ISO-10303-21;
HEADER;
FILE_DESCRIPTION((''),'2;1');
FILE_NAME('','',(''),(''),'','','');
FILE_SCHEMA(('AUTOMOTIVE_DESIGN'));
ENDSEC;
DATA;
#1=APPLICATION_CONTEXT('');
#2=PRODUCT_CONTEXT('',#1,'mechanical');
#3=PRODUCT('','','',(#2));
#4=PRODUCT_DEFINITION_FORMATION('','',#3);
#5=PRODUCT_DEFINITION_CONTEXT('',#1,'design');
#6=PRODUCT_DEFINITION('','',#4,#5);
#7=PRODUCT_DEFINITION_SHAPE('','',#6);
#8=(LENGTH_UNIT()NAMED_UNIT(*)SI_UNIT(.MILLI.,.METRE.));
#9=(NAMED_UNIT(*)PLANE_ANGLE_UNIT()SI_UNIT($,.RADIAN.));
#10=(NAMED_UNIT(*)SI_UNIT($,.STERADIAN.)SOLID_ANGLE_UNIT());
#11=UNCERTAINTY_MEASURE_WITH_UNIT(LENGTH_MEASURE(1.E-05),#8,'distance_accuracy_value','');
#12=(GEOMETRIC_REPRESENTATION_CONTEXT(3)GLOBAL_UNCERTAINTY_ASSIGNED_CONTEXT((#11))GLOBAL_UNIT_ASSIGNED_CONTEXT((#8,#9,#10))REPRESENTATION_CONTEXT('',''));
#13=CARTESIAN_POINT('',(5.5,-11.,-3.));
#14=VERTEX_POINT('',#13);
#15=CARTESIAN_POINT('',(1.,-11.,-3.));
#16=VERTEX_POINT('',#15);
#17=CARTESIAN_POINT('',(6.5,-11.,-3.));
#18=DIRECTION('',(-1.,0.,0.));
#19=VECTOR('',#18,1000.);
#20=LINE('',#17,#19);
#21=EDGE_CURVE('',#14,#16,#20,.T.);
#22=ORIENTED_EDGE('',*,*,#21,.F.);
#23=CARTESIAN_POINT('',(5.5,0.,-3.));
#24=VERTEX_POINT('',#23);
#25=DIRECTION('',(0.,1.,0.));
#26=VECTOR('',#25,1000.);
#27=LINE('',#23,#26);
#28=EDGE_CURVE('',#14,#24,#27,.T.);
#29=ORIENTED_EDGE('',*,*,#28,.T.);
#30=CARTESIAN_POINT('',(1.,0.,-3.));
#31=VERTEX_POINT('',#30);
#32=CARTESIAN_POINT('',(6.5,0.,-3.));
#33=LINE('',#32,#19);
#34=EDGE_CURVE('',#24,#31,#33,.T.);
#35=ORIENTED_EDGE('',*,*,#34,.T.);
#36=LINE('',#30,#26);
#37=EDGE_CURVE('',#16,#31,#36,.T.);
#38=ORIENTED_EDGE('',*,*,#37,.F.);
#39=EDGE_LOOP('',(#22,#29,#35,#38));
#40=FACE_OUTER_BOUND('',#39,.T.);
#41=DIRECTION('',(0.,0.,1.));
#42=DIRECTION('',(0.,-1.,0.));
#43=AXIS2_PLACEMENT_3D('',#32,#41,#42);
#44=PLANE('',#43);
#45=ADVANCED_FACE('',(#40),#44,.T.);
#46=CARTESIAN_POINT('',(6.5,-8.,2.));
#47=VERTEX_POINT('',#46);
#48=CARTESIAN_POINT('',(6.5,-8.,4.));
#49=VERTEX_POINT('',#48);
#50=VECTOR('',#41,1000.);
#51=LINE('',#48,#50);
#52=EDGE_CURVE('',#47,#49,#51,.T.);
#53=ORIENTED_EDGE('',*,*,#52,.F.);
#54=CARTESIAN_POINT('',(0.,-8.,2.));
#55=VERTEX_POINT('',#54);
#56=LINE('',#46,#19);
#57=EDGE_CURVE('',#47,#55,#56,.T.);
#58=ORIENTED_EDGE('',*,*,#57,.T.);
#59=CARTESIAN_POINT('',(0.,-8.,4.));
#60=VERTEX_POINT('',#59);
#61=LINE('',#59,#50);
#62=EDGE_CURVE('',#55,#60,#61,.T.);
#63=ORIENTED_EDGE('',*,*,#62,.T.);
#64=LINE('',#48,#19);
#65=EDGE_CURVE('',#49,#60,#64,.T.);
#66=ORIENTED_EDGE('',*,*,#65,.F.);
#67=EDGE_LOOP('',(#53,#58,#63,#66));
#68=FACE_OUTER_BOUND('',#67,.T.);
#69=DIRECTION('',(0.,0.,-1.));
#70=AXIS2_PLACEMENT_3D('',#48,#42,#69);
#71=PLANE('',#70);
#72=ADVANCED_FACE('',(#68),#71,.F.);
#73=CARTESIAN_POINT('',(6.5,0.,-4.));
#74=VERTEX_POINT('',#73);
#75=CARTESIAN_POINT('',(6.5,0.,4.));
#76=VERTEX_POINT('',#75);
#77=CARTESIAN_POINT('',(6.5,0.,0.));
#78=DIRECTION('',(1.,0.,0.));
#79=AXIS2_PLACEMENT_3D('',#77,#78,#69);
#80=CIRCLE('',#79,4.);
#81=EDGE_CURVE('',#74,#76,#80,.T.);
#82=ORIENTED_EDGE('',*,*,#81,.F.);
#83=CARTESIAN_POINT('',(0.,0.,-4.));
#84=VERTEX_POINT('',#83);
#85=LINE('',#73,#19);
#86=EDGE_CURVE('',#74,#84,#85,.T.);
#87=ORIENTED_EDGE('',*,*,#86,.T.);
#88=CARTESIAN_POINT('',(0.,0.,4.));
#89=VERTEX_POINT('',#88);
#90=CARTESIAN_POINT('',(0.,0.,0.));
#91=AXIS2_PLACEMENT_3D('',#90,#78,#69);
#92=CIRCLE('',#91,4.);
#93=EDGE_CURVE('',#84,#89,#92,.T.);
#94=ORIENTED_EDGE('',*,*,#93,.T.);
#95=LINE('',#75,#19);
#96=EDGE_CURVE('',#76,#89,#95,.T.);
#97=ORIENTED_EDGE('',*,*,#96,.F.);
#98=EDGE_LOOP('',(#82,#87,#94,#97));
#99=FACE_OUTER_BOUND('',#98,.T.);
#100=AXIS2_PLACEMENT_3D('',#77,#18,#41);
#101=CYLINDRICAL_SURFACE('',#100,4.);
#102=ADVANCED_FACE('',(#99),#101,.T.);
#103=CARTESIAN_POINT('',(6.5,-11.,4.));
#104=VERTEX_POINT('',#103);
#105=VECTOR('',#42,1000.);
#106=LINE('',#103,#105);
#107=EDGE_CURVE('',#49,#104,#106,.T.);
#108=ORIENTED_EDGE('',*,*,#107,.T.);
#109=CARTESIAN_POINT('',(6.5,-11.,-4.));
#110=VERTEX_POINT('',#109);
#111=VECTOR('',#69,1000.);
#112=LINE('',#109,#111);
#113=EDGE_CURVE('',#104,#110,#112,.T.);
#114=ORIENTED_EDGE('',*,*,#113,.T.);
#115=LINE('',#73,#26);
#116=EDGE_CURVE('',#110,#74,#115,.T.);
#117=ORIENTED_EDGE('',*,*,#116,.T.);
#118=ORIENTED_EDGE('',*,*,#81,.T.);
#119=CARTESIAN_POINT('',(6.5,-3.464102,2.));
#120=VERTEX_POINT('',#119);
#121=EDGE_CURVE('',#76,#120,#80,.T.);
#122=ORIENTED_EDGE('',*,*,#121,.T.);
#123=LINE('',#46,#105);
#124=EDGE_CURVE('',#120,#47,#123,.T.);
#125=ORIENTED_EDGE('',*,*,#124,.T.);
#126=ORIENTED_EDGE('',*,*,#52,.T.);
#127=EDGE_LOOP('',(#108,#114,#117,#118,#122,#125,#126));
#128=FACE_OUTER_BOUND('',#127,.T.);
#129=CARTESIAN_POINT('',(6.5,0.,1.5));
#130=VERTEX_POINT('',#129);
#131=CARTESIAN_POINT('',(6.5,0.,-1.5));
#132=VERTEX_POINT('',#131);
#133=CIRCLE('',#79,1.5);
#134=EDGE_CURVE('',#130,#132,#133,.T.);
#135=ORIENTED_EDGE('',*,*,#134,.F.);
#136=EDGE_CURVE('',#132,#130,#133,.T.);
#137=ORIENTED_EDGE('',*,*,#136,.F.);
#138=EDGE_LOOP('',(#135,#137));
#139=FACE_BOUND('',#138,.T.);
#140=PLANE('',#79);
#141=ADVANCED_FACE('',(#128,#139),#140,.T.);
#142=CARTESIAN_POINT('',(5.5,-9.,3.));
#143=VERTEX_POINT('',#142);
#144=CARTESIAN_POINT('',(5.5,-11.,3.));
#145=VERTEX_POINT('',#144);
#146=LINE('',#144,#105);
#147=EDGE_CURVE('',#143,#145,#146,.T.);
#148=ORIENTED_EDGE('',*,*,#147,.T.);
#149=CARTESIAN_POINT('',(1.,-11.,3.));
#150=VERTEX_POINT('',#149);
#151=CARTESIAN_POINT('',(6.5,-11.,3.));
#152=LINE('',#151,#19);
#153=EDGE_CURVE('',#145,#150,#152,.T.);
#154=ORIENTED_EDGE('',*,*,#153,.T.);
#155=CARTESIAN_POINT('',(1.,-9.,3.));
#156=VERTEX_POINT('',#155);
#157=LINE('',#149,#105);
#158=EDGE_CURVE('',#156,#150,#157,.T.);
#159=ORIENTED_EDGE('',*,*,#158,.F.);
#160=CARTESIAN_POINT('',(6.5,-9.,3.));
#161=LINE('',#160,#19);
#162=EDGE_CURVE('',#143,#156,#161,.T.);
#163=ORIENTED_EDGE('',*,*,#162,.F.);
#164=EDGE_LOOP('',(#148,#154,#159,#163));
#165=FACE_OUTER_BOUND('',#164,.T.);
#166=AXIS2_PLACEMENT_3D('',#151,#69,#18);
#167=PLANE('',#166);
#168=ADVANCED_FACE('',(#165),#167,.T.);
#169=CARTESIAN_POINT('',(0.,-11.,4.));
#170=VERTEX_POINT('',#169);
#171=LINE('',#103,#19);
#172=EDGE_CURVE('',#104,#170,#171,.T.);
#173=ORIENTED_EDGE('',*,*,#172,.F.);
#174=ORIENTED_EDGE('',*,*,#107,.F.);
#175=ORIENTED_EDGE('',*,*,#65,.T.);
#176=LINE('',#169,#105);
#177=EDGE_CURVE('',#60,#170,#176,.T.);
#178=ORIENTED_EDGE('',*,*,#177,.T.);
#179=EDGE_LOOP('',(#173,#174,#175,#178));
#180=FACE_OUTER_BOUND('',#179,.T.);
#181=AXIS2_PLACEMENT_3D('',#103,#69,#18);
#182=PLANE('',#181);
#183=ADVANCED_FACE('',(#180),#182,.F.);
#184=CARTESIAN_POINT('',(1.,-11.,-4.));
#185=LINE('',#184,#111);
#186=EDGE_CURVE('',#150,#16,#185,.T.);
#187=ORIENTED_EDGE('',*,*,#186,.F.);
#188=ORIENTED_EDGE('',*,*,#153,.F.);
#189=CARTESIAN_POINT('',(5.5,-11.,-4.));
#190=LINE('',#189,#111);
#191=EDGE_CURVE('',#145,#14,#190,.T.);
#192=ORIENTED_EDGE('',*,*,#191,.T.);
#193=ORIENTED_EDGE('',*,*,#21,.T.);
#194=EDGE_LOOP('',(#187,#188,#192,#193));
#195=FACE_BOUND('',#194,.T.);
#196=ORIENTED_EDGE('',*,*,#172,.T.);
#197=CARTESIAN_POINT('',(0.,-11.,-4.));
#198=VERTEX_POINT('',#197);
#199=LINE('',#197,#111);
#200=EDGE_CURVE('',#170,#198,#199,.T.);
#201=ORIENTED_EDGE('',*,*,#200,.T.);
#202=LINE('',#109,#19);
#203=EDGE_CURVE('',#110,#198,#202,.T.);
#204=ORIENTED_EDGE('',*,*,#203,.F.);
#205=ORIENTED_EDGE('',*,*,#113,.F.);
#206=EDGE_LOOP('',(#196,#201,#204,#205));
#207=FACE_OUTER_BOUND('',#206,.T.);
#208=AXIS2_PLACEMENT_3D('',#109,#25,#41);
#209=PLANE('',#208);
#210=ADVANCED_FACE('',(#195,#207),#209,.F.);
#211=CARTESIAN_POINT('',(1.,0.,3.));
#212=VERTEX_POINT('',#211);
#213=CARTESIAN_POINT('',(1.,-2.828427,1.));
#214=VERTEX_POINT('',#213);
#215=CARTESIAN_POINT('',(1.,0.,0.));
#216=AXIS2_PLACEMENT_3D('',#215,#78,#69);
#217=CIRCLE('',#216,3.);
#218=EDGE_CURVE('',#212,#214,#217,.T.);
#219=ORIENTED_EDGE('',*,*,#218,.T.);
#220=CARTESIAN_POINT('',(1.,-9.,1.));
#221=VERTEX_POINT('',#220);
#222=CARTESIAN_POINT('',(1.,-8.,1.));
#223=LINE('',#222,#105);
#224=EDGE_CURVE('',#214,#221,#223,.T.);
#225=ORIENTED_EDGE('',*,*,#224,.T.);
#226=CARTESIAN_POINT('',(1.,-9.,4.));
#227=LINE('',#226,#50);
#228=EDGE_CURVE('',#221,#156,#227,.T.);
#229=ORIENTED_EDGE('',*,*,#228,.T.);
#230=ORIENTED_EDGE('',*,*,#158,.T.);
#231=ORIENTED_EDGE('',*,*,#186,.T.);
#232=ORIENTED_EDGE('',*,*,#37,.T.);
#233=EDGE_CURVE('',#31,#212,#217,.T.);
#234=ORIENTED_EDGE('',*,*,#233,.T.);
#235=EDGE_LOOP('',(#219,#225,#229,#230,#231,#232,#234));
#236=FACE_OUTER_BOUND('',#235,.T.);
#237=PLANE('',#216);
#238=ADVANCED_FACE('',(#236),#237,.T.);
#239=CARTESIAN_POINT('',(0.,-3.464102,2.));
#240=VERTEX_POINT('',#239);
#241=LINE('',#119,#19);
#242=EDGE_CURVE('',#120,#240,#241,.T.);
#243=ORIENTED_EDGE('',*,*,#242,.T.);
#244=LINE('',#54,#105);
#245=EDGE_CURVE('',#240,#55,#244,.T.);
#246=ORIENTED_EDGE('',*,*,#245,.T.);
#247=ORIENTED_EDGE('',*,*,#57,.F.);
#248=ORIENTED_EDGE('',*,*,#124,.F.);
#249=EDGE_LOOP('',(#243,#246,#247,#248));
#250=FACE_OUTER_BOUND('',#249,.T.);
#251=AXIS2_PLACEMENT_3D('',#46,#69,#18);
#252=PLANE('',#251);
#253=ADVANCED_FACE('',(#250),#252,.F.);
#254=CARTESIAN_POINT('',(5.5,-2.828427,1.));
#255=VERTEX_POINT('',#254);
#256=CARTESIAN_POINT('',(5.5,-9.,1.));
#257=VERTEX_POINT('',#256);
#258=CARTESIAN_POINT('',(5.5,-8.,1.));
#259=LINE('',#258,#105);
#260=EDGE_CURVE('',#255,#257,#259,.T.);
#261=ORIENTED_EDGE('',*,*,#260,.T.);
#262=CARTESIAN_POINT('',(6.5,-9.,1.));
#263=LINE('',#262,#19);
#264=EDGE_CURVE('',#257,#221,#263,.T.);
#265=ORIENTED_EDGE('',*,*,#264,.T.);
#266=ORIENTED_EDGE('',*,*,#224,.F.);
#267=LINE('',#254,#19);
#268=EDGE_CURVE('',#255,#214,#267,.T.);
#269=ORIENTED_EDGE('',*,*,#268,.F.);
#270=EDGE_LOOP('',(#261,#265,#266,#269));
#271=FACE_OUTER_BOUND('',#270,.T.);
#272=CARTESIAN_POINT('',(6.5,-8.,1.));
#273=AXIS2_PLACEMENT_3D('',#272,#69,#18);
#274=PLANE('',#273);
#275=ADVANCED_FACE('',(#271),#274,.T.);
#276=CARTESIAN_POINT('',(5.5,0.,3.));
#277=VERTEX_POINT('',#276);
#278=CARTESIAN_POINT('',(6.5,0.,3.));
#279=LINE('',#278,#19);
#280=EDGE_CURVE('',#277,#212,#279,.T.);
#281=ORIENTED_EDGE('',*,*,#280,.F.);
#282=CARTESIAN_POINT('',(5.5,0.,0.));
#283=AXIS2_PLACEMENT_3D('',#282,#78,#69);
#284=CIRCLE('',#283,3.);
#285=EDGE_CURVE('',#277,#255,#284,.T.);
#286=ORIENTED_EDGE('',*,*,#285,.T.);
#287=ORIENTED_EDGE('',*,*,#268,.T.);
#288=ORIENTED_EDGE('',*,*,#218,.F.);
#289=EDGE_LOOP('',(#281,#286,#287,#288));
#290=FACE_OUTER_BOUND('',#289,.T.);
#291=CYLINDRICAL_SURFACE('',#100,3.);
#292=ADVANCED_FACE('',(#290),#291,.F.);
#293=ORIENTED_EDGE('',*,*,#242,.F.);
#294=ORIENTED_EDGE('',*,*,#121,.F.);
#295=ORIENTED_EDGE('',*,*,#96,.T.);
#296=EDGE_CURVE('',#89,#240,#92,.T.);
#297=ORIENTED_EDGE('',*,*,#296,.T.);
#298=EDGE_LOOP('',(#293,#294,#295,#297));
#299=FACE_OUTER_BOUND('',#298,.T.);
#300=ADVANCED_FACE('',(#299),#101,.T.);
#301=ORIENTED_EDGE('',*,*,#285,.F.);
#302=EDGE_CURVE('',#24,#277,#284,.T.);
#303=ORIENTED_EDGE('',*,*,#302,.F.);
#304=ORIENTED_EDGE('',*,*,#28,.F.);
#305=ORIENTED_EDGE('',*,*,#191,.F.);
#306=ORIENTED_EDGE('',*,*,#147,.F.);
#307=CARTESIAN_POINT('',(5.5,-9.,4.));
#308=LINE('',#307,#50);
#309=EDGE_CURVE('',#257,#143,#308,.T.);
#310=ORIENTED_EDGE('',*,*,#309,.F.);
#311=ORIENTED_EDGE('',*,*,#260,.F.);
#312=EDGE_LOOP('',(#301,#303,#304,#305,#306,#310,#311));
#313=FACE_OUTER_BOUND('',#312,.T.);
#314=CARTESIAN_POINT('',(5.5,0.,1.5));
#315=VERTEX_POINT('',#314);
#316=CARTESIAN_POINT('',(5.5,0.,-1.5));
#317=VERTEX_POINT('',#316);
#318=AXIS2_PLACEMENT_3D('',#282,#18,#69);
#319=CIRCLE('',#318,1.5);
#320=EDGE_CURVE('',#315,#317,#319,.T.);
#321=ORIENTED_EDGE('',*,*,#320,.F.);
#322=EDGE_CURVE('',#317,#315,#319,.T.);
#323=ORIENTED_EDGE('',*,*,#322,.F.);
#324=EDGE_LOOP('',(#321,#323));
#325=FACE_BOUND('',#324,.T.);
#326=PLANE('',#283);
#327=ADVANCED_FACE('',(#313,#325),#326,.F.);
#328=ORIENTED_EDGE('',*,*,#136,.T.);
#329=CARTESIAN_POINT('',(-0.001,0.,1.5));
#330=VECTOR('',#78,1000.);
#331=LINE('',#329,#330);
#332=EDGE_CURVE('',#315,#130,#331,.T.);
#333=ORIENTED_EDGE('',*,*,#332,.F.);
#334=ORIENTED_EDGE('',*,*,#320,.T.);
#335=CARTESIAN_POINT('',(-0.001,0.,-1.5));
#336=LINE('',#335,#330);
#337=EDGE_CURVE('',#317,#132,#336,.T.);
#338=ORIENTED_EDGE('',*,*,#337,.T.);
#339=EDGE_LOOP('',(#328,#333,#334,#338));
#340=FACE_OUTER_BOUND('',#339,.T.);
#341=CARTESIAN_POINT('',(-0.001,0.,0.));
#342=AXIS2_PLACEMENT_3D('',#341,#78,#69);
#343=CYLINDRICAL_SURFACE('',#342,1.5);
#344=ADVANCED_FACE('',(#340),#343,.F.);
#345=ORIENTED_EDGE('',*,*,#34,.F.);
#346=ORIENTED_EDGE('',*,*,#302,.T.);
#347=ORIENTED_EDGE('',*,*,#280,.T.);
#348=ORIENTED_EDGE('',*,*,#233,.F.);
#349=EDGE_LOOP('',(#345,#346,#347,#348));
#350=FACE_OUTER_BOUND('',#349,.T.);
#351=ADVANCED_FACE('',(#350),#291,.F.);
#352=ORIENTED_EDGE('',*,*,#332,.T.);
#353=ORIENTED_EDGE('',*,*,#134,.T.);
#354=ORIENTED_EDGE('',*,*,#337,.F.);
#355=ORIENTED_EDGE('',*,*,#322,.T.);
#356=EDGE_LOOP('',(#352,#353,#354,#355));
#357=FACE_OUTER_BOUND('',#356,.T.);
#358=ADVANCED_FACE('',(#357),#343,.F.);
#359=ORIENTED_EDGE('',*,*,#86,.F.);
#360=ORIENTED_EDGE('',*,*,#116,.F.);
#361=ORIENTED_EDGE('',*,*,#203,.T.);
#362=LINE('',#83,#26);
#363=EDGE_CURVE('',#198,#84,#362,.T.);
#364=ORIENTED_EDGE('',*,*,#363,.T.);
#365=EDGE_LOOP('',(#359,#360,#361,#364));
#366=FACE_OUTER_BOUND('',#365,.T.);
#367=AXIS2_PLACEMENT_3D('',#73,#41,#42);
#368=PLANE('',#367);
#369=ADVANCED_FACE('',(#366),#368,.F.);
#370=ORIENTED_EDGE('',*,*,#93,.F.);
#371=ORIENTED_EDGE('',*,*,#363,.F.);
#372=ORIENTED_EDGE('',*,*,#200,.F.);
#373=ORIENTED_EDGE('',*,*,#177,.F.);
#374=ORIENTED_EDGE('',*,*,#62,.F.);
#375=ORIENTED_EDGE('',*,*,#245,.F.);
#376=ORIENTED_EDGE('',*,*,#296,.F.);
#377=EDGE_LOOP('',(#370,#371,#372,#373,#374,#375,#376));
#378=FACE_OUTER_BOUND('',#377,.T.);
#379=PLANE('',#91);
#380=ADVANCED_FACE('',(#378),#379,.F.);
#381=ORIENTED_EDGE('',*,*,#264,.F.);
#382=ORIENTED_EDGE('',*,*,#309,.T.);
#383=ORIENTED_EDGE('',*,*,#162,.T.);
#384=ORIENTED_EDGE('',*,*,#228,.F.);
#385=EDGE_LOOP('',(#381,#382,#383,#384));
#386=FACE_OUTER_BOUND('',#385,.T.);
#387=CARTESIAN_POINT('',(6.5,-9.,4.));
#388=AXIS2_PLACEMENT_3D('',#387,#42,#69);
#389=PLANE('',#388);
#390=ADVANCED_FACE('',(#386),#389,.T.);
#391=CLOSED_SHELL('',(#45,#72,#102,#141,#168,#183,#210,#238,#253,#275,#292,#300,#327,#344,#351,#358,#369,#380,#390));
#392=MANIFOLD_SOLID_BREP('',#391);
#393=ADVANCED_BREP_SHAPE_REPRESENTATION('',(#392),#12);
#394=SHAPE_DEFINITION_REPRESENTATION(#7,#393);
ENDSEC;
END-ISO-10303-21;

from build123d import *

# Parameters (mm, degrees)
LEG_BODY_DEPTH        = 6.5
LEG_SHELL_1MM_T       = -1
HIP_PIN_HOLE_REACH    = 15.388
HIP_PIN_HOLE_SKETCH_R = 1.5


with BuildPart() as part:
    # Leg Profile Sketch → Leg Body (new body)
    with BuildSketch(Plane(origin=(0, 0, 0), x_dir=(0, 0, -1), z_dir=(1, 0, 0))):
        with BuildLine():
            Line((4, 0), (4, -11))
            Line((4, -11), (-4, -11))
            Line((-4, -11), (-4, -8))
            Line((-4, -8), (-2, -8))
            Line((-2, -8), (-2, -3.464101615))
            ThreePointArc((-2, -3.464101615), (-2, 3.464101615), (4, 0))
        make_face()
    extrude(amount=LEG_BODY_DEPTH)

    # Leg Shell 1mm
    leg_shell_1mm_openings = [part.faces().sort_by_distance(p)[0] for p in [
        (3.25, -11, 0),
    ]]
    offset(amount=LEG_SHELL_1MM_T, openings=leg_shell_1mm_openings, kind=Kind.INTERSECTION)

    # Hip Pin Hole Sketch → Hip Pin Hole (cut, up to next)
    with BuildSketch(Plane(origin=(6.5, 0, 0), x_dir=(0, 0, -1), z_dir=(1, 0, 0)), mode=Mode.PRIVATE) as hip_pin_hole_sk1:
        Circle(HIP_PIN_HOLE_SKETCH_R)
    hip_pin_hole_tool1 = extrude(hip_pin_hole_sk1.sketch, amount=-HIP_PIN_HOLE_REACH, mode=Mode.PRIVATE) & part.part
    add(hip_pin_hole_tool1.solids().sort_by_distance((6.5, 0, 0))[0], mode=Mode.SUBTRACT)


solid = part.part
